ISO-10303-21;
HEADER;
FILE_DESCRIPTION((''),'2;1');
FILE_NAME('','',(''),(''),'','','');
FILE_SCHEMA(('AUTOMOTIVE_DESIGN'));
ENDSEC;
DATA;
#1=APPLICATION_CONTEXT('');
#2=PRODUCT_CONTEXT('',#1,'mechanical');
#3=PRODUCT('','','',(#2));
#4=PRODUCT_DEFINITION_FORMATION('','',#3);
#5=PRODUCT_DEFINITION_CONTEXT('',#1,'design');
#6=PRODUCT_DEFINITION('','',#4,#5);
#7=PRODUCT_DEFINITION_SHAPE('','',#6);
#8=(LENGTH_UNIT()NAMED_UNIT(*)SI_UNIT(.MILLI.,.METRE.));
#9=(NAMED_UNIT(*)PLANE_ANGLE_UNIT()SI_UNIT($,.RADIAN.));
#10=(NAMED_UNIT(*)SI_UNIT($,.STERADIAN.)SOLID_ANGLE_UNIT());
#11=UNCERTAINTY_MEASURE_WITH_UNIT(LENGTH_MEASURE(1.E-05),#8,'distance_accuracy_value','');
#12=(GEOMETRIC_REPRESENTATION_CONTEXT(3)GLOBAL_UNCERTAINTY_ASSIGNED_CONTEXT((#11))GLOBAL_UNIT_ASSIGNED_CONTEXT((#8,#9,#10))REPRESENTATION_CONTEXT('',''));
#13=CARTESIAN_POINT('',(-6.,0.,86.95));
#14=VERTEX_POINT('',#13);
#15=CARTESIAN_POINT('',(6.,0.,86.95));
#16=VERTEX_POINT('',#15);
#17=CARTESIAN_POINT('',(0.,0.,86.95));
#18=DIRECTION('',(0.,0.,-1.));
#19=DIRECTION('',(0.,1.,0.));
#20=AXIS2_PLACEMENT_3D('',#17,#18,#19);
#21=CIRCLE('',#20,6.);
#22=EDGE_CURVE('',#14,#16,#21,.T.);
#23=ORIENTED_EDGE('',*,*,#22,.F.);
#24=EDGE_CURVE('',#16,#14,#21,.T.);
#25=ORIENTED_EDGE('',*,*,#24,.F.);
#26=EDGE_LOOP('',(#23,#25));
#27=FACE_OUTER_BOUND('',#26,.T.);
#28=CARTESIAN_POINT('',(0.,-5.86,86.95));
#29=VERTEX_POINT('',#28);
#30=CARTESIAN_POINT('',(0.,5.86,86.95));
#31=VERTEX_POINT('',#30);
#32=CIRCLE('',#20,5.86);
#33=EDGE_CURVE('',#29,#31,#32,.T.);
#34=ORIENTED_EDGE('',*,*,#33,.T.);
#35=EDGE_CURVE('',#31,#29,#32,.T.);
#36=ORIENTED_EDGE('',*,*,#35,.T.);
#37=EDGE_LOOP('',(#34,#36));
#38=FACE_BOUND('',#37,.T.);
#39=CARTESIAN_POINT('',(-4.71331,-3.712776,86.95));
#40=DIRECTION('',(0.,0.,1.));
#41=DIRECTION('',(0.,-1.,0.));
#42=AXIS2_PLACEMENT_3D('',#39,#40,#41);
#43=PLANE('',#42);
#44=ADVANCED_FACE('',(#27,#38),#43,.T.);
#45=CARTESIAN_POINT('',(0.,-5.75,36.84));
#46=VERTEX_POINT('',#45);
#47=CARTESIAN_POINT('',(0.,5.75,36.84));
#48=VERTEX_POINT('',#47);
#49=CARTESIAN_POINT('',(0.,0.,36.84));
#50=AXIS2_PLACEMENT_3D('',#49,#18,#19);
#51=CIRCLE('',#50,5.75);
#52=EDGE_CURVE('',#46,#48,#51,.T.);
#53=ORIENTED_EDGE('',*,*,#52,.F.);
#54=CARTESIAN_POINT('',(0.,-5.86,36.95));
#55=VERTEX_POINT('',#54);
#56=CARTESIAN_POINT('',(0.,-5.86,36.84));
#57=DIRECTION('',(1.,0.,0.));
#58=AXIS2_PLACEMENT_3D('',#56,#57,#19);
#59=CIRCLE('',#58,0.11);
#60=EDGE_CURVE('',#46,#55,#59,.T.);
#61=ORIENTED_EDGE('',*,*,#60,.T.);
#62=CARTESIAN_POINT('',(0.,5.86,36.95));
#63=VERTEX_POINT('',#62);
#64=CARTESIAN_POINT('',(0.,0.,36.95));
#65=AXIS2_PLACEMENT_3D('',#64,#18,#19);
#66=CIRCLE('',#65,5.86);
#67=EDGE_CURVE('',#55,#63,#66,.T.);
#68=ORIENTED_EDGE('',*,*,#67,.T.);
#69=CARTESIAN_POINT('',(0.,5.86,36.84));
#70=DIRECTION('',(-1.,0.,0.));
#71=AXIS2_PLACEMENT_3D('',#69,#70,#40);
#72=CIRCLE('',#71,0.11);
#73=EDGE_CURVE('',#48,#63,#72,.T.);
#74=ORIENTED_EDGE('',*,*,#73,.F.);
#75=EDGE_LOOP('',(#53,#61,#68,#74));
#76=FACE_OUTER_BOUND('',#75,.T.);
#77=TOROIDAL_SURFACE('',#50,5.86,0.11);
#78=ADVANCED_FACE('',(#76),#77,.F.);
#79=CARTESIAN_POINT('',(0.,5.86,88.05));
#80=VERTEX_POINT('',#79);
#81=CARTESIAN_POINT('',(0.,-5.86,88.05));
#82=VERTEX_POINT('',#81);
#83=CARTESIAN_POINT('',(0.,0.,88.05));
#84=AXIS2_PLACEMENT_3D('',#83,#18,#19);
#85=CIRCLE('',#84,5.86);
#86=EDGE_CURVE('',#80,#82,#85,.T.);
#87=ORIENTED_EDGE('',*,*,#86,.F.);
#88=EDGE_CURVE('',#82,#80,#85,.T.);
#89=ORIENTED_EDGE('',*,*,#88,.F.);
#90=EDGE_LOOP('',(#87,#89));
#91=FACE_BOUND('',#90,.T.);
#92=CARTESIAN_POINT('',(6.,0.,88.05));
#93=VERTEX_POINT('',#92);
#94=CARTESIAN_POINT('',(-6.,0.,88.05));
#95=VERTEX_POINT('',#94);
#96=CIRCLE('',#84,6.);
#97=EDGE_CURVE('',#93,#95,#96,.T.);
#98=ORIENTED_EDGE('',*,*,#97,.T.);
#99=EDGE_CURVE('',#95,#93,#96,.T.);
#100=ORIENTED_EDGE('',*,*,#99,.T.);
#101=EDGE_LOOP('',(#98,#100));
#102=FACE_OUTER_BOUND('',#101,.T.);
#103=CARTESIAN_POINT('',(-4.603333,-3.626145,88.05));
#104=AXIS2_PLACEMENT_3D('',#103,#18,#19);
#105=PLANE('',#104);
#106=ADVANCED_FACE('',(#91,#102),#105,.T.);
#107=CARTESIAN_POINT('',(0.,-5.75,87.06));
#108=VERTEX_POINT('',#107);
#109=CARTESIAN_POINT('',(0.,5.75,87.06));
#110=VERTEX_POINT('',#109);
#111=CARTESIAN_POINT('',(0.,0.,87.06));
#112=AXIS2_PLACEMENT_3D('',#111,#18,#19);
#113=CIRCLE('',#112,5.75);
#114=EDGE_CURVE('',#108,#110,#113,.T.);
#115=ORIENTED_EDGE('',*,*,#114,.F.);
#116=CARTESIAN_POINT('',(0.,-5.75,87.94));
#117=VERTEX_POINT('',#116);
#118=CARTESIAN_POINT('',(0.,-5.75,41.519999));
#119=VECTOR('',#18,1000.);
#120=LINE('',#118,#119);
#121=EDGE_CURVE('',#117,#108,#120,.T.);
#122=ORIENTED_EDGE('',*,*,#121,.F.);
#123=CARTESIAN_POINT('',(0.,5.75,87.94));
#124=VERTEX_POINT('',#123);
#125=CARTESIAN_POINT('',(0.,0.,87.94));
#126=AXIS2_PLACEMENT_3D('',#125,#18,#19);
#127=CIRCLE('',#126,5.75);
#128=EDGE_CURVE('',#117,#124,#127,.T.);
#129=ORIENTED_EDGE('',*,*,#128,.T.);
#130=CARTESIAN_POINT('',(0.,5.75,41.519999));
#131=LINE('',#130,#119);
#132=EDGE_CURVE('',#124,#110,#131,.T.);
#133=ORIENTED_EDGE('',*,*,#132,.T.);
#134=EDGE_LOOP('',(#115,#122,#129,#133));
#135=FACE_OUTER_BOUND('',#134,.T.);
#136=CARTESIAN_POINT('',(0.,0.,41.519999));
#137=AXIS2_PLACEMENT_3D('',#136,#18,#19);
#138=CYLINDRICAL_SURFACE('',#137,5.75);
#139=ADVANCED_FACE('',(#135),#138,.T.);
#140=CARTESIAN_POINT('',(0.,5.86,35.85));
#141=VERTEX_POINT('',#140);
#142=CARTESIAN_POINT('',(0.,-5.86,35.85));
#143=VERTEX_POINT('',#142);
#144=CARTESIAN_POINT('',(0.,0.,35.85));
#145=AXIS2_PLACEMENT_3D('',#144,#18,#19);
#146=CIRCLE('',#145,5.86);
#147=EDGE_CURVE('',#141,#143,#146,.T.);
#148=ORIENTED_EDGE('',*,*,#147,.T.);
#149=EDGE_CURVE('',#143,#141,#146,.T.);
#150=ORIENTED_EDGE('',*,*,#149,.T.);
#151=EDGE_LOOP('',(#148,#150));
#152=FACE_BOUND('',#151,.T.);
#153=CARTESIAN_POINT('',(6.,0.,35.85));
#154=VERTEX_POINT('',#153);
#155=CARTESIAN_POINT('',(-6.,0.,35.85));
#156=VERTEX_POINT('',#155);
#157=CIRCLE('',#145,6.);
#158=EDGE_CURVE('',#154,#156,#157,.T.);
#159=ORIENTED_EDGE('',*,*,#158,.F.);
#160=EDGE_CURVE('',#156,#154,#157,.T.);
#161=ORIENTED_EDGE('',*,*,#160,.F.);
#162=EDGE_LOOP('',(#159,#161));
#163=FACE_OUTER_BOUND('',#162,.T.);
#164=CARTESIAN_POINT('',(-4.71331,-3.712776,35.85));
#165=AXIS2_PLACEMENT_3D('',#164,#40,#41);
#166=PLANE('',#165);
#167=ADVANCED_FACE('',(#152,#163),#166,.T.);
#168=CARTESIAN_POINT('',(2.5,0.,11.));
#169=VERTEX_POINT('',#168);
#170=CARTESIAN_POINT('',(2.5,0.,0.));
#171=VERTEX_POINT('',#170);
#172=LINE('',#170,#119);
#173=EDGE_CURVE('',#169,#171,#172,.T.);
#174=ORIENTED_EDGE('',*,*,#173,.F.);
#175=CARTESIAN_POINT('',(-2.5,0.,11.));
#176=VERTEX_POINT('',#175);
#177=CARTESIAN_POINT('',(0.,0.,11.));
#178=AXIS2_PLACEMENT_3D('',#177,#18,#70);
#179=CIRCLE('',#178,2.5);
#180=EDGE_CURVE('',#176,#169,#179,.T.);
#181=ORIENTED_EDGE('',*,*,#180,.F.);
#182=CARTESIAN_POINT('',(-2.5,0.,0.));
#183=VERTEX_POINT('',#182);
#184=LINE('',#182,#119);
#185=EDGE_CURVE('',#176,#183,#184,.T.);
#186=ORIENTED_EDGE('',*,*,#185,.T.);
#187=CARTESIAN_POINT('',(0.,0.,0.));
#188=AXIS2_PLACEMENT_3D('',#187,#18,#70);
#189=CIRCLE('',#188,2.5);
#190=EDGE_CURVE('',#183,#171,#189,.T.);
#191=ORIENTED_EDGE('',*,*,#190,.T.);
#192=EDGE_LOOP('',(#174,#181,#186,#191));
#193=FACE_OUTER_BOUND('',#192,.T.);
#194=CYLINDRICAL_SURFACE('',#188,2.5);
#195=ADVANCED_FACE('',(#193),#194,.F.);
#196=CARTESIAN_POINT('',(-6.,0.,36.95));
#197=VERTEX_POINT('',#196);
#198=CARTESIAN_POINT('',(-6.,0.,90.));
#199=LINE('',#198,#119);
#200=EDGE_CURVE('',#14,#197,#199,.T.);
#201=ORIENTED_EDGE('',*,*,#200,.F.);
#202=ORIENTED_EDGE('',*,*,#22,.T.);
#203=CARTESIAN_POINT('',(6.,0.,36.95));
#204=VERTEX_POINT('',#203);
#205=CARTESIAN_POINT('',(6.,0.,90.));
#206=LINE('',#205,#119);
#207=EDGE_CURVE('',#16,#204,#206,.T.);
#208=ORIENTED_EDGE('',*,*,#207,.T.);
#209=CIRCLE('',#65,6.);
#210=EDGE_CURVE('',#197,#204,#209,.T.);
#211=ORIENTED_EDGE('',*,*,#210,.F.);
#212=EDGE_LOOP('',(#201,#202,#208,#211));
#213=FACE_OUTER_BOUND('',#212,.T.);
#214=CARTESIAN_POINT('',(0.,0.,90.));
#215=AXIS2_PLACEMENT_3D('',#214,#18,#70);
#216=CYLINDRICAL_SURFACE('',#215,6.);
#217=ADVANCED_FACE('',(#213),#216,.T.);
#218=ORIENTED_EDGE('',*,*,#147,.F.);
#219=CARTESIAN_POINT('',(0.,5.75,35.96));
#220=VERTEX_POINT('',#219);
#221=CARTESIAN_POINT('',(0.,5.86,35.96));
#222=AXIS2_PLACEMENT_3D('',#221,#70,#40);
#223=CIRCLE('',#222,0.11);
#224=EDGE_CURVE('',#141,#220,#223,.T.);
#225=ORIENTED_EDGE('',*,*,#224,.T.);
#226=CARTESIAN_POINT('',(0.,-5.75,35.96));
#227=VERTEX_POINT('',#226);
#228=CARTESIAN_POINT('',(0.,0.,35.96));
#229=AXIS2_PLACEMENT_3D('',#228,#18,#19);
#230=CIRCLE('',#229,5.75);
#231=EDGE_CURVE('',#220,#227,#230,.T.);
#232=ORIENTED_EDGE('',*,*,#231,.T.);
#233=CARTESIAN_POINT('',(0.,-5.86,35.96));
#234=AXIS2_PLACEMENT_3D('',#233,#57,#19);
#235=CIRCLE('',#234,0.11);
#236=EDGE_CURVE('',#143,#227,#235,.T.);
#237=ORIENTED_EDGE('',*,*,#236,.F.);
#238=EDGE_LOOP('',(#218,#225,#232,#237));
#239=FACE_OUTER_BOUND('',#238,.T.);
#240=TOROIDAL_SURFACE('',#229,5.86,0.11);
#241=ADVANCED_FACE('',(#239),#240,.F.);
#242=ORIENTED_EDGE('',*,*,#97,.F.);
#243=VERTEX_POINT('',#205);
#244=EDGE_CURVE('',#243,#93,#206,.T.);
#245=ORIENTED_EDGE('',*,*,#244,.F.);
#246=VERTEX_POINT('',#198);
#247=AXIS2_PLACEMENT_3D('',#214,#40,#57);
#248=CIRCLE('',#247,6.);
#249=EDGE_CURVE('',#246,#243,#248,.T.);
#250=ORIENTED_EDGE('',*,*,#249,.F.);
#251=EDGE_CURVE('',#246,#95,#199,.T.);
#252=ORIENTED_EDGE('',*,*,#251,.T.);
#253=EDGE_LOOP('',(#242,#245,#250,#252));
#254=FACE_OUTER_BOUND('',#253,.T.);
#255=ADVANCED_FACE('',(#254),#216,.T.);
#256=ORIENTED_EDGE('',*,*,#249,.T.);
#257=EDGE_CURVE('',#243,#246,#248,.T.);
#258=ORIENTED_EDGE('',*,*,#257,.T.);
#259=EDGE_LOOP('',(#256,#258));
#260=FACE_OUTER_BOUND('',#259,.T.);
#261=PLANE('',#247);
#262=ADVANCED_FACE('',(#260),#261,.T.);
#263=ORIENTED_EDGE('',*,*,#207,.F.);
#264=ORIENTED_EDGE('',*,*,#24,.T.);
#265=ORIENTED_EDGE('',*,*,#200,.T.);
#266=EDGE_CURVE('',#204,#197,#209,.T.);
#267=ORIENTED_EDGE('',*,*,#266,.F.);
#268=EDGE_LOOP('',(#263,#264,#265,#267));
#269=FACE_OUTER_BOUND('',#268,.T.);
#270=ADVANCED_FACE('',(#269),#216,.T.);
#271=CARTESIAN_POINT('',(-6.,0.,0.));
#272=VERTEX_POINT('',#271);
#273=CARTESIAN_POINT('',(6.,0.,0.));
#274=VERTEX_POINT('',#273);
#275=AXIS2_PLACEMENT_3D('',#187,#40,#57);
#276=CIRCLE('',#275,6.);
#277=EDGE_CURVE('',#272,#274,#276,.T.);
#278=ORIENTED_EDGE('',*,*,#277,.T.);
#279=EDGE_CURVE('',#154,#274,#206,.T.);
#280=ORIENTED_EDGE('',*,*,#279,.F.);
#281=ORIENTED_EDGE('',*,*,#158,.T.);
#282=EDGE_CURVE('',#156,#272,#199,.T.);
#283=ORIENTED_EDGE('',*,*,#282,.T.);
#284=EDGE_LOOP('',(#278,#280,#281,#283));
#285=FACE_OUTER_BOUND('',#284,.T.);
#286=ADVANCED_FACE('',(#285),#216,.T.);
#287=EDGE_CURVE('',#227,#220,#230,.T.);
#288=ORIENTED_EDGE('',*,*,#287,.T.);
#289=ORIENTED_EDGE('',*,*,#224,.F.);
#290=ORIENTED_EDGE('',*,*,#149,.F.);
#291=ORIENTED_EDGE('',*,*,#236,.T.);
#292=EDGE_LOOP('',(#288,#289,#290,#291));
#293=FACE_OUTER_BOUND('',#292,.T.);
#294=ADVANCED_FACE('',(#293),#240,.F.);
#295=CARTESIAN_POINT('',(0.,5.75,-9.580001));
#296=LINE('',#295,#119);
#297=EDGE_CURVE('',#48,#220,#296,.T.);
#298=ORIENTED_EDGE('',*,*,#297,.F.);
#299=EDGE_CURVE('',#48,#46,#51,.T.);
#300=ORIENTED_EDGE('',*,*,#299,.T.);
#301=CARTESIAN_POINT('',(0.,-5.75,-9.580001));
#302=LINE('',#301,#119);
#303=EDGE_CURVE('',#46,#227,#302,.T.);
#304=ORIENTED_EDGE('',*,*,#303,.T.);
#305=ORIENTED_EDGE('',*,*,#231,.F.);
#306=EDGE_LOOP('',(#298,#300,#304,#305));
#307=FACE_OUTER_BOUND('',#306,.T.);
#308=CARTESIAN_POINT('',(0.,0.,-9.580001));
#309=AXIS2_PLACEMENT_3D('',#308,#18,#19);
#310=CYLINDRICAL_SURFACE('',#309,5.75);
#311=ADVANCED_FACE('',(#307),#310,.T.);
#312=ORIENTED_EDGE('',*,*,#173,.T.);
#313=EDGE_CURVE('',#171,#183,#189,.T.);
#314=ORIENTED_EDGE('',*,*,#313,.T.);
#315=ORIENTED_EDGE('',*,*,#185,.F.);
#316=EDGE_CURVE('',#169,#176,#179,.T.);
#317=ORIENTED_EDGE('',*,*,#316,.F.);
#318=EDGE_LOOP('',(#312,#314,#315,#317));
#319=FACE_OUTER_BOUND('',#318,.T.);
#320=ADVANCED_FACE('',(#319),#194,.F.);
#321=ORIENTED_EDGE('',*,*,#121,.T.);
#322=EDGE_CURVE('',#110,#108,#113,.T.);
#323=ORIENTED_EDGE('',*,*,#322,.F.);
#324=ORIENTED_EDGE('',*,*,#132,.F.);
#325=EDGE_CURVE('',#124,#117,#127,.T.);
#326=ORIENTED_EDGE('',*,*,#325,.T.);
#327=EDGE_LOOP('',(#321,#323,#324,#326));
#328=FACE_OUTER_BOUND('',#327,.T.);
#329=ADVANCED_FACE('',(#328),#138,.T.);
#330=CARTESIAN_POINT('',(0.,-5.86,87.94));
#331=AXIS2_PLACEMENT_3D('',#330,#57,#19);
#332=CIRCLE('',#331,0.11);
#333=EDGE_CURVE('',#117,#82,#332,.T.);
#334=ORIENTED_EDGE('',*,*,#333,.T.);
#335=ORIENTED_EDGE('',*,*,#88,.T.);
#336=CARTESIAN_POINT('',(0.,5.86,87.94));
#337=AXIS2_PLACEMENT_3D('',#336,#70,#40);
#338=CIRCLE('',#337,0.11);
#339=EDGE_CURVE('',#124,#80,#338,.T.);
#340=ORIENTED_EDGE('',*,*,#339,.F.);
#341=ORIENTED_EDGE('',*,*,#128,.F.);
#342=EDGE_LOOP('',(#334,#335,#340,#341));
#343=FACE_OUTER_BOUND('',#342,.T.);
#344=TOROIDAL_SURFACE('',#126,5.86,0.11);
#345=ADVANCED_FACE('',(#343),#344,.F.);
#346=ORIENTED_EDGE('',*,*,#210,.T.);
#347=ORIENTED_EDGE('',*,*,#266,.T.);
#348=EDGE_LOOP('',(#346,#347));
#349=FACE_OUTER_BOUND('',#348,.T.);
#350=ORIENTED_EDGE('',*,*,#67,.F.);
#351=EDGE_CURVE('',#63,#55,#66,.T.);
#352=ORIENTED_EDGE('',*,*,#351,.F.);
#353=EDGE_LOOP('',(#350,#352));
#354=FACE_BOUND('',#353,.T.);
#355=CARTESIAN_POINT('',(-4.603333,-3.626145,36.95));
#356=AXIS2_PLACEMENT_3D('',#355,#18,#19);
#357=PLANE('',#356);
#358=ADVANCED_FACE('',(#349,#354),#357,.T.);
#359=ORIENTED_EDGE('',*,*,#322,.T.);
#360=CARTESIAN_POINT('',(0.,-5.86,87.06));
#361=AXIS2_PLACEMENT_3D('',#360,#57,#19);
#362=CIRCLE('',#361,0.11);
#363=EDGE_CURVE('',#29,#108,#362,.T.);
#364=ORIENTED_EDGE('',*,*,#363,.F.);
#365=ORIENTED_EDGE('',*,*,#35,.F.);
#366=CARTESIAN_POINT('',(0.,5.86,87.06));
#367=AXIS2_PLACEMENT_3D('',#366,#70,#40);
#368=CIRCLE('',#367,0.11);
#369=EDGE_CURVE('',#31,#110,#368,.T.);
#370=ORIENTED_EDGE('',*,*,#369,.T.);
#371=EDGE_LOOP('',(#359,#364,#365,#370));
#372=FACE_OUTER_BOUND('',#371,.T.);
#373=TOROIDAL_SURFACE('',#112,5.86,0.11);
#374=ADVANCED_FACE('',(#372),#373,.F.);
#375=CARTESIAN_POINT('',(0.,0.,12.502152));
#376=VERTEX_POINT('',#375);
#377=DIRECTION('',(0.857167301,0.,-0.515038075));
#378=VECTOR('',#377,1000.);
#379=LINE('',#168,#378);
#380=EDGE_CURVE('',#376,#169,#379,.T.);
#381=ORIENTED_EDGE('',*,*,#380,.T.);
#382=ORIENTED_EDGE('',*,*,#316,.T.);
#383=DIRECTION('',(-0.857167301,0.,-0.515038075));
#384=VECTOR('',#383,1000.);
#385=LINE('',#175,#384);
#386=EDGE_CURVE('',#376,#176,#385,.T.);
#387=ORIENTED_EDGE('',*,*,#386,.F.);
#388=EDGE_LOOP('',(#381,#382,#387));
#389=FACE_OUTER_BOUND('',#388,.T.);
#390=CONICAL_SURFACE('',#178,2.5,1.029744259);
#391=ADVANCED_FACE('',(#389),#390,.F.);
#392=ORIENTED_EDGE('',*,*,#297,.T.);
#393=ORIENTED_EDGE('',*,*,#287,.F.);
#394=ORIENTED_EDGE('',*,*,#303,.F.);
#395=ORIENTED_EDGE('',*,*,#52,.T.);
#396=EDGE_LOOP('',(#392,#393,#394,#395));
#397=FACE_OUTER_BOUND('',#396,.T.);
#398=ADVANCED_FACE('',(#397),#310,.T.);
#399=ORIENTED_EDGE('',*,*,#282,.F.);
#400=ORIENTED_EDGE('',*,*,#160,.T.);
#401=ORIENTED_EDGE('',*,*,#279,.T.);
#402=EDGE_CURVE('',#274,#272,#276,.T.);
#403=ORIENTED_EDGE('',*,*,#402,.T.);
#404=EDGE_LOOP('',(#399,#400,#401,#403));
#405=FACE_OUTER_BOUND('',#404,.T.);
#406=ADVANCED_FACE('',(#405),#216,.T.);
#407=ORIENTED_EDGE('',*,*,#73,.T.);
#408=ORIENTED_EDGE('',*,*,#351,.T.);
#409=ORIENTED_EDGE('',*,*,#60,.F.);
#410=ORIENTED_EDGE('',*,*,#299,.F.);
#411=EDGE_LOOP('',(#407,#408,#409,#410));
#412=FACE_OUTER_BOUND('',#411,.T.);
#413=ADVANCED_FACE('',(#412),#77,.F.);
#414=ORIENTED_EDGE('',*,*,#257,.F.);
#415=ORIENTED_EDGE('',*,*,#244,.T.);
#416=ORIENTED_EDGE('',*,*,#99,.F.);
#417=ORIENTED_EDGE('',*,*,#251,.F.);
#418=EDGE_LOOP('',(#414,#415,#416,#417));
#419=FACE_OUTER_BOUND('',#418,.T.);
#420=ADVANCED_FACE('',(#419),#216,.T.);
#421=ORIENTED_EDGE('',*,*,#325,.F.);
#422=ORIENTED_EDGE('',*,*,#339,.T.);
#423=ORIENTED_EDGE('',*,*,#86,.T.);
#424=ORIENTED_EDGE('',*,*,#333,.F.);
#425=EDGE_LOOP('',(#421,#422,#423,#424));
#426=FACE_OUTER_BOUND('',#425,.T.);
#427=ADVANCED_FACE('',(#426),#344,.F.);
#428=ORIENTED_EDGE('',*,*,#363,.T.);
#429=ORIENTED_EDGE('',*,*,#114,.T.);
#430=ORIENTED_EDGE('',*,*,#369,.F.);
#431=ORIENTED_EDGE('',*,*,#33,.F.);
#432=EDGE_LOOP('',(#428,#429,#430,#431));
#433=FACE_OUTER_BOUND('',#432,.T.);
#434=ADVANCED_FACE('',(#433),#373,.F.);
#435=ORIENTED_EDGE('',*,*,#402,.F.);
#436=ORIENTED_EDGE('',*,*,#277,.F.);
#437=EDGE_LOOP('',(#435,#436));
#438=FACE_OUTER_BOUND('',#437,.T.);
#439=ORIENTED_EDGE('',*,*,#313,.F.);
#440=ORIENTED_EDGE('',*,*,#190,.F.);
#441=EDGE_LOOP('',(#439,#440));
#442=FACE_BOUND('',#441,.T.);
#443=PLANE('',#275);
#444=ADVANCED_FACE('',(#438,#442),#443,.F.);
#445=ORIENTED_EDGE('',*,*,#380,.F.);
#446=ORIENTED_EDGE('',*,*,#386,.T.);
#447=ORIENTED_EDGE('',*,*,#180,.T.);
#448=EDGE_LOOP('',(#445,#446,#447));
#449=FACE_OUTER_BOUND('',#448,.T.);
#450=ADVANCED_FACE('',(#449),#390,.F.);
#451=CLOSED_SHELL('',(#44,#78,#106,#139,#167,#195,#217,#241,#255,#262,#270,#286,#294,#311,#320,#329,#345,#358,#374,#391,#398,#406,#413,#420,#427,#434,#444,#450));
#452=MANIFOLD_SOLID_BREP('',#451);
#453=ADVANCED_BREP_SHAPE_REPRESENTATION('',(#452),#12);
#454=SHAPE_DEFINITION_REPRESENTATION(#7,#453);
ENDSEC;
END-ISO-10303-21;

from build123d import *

# Parameters (mm, degrees)
SKETCH_1_R             = 6
EXTRUDE_1_DEPTH        = 90
PATTERN_LINEAR_1_COUNT = 2
PATTERN_LINEAR_1_PITCH = 51.1
HOLE_WIZARD_M6_1_D     = 5
HOLE_WIZARD_M6_1_DEPTH = 11
HOLE_WIZARD_M6_1_TIP   = 1.502151548


with BuildPart() as part:
    # 草图1 → 凸台-拉伸1 (new body)
    with BuildSketch(Plane.XY):
        with Locations(Location((0, 0, 0), (0, 0, 180))):
            Circle(SKETCH_1_R)
    extrude(amount=EXTRUDE_1_DEPTH)

    # Groove Sketch → Retaining Ring Groove (revolve, cut)
    with BuildSketch(Plane(origin=(4.683915956, 3.689622128, 8.399116992), x_dir=(-0.5195228612321346, -0.40923941910457057, 0.7500793921366791), z_dir=(0.6187960743401806, -0.785551664998033, 0)), mode=Mode.PRIVATE) as retaining_ring_groove_sk:
        with BuildLine():
            Line((67.563324222, -43.809060949), (67.655912914, -43.704049834))
            Line((67.655912914, -43.704049834), (66.830825582, -42.97656726))
            Line((66.830825582, -42.97656726), (66.738236891, -43.081578375))
            ThreePointArc((66.738236891, -43.081578375), (66.710962353, -43.161228331), (66.747997367, -43.236835366))
            Line((66.747997367, -43.236835366), (67.408067232, -43.818821425))
            ThreePointArc((67.408067232, -43.818821425), (67.487717188, -43.846095963), (67.563324222, -43.809060949))
        make_face()
    retaining_ring_groove = revolve(retaining_ring_groove_sk.sketch.rotate(Axis((0, 0, 41.519998945), (0, 0, -1)), 128.228270648), axis=Axis((0, 0, 41.519998945), (0, 0, -1)), mode=Mode.SUBTRACT)

    # 阵列(线性)1: Retaining Ring Groove ×2
    with Locations(*[(0, 0, -i * PATTERN_LINEAR_1_PITCH) for i in range(1, PATTERN_LINEAR_1_COUNT)]):
        add(retaining_ring_groove, mode=Mode.SUBTRACT)

    # M6 螺纹孔1
    with Locations(Plane(origin=(0, 0, 0), x_dir=(-1, 0, 0), z_dir=(0, 0, -1))):
        with Locations((0, 0)):
            Hole(HOLE_WIZARD_M6_1_D / 2, depth=HOLE_WIZARD_M6_1_DEPTH)
            with Locations((0, 0, -(HOLE_WIZARD_M6_1_DEPTH + HOLE_WIZARD_M6_1_TIP / 2))):  # 118° drill point
                Cone(0, HOLE_WIZARD_M6_1_D / 2, HOLE_WIZARD_M6_1_TIP, mode=Mode.SUBTRACT)


solid = part.part
